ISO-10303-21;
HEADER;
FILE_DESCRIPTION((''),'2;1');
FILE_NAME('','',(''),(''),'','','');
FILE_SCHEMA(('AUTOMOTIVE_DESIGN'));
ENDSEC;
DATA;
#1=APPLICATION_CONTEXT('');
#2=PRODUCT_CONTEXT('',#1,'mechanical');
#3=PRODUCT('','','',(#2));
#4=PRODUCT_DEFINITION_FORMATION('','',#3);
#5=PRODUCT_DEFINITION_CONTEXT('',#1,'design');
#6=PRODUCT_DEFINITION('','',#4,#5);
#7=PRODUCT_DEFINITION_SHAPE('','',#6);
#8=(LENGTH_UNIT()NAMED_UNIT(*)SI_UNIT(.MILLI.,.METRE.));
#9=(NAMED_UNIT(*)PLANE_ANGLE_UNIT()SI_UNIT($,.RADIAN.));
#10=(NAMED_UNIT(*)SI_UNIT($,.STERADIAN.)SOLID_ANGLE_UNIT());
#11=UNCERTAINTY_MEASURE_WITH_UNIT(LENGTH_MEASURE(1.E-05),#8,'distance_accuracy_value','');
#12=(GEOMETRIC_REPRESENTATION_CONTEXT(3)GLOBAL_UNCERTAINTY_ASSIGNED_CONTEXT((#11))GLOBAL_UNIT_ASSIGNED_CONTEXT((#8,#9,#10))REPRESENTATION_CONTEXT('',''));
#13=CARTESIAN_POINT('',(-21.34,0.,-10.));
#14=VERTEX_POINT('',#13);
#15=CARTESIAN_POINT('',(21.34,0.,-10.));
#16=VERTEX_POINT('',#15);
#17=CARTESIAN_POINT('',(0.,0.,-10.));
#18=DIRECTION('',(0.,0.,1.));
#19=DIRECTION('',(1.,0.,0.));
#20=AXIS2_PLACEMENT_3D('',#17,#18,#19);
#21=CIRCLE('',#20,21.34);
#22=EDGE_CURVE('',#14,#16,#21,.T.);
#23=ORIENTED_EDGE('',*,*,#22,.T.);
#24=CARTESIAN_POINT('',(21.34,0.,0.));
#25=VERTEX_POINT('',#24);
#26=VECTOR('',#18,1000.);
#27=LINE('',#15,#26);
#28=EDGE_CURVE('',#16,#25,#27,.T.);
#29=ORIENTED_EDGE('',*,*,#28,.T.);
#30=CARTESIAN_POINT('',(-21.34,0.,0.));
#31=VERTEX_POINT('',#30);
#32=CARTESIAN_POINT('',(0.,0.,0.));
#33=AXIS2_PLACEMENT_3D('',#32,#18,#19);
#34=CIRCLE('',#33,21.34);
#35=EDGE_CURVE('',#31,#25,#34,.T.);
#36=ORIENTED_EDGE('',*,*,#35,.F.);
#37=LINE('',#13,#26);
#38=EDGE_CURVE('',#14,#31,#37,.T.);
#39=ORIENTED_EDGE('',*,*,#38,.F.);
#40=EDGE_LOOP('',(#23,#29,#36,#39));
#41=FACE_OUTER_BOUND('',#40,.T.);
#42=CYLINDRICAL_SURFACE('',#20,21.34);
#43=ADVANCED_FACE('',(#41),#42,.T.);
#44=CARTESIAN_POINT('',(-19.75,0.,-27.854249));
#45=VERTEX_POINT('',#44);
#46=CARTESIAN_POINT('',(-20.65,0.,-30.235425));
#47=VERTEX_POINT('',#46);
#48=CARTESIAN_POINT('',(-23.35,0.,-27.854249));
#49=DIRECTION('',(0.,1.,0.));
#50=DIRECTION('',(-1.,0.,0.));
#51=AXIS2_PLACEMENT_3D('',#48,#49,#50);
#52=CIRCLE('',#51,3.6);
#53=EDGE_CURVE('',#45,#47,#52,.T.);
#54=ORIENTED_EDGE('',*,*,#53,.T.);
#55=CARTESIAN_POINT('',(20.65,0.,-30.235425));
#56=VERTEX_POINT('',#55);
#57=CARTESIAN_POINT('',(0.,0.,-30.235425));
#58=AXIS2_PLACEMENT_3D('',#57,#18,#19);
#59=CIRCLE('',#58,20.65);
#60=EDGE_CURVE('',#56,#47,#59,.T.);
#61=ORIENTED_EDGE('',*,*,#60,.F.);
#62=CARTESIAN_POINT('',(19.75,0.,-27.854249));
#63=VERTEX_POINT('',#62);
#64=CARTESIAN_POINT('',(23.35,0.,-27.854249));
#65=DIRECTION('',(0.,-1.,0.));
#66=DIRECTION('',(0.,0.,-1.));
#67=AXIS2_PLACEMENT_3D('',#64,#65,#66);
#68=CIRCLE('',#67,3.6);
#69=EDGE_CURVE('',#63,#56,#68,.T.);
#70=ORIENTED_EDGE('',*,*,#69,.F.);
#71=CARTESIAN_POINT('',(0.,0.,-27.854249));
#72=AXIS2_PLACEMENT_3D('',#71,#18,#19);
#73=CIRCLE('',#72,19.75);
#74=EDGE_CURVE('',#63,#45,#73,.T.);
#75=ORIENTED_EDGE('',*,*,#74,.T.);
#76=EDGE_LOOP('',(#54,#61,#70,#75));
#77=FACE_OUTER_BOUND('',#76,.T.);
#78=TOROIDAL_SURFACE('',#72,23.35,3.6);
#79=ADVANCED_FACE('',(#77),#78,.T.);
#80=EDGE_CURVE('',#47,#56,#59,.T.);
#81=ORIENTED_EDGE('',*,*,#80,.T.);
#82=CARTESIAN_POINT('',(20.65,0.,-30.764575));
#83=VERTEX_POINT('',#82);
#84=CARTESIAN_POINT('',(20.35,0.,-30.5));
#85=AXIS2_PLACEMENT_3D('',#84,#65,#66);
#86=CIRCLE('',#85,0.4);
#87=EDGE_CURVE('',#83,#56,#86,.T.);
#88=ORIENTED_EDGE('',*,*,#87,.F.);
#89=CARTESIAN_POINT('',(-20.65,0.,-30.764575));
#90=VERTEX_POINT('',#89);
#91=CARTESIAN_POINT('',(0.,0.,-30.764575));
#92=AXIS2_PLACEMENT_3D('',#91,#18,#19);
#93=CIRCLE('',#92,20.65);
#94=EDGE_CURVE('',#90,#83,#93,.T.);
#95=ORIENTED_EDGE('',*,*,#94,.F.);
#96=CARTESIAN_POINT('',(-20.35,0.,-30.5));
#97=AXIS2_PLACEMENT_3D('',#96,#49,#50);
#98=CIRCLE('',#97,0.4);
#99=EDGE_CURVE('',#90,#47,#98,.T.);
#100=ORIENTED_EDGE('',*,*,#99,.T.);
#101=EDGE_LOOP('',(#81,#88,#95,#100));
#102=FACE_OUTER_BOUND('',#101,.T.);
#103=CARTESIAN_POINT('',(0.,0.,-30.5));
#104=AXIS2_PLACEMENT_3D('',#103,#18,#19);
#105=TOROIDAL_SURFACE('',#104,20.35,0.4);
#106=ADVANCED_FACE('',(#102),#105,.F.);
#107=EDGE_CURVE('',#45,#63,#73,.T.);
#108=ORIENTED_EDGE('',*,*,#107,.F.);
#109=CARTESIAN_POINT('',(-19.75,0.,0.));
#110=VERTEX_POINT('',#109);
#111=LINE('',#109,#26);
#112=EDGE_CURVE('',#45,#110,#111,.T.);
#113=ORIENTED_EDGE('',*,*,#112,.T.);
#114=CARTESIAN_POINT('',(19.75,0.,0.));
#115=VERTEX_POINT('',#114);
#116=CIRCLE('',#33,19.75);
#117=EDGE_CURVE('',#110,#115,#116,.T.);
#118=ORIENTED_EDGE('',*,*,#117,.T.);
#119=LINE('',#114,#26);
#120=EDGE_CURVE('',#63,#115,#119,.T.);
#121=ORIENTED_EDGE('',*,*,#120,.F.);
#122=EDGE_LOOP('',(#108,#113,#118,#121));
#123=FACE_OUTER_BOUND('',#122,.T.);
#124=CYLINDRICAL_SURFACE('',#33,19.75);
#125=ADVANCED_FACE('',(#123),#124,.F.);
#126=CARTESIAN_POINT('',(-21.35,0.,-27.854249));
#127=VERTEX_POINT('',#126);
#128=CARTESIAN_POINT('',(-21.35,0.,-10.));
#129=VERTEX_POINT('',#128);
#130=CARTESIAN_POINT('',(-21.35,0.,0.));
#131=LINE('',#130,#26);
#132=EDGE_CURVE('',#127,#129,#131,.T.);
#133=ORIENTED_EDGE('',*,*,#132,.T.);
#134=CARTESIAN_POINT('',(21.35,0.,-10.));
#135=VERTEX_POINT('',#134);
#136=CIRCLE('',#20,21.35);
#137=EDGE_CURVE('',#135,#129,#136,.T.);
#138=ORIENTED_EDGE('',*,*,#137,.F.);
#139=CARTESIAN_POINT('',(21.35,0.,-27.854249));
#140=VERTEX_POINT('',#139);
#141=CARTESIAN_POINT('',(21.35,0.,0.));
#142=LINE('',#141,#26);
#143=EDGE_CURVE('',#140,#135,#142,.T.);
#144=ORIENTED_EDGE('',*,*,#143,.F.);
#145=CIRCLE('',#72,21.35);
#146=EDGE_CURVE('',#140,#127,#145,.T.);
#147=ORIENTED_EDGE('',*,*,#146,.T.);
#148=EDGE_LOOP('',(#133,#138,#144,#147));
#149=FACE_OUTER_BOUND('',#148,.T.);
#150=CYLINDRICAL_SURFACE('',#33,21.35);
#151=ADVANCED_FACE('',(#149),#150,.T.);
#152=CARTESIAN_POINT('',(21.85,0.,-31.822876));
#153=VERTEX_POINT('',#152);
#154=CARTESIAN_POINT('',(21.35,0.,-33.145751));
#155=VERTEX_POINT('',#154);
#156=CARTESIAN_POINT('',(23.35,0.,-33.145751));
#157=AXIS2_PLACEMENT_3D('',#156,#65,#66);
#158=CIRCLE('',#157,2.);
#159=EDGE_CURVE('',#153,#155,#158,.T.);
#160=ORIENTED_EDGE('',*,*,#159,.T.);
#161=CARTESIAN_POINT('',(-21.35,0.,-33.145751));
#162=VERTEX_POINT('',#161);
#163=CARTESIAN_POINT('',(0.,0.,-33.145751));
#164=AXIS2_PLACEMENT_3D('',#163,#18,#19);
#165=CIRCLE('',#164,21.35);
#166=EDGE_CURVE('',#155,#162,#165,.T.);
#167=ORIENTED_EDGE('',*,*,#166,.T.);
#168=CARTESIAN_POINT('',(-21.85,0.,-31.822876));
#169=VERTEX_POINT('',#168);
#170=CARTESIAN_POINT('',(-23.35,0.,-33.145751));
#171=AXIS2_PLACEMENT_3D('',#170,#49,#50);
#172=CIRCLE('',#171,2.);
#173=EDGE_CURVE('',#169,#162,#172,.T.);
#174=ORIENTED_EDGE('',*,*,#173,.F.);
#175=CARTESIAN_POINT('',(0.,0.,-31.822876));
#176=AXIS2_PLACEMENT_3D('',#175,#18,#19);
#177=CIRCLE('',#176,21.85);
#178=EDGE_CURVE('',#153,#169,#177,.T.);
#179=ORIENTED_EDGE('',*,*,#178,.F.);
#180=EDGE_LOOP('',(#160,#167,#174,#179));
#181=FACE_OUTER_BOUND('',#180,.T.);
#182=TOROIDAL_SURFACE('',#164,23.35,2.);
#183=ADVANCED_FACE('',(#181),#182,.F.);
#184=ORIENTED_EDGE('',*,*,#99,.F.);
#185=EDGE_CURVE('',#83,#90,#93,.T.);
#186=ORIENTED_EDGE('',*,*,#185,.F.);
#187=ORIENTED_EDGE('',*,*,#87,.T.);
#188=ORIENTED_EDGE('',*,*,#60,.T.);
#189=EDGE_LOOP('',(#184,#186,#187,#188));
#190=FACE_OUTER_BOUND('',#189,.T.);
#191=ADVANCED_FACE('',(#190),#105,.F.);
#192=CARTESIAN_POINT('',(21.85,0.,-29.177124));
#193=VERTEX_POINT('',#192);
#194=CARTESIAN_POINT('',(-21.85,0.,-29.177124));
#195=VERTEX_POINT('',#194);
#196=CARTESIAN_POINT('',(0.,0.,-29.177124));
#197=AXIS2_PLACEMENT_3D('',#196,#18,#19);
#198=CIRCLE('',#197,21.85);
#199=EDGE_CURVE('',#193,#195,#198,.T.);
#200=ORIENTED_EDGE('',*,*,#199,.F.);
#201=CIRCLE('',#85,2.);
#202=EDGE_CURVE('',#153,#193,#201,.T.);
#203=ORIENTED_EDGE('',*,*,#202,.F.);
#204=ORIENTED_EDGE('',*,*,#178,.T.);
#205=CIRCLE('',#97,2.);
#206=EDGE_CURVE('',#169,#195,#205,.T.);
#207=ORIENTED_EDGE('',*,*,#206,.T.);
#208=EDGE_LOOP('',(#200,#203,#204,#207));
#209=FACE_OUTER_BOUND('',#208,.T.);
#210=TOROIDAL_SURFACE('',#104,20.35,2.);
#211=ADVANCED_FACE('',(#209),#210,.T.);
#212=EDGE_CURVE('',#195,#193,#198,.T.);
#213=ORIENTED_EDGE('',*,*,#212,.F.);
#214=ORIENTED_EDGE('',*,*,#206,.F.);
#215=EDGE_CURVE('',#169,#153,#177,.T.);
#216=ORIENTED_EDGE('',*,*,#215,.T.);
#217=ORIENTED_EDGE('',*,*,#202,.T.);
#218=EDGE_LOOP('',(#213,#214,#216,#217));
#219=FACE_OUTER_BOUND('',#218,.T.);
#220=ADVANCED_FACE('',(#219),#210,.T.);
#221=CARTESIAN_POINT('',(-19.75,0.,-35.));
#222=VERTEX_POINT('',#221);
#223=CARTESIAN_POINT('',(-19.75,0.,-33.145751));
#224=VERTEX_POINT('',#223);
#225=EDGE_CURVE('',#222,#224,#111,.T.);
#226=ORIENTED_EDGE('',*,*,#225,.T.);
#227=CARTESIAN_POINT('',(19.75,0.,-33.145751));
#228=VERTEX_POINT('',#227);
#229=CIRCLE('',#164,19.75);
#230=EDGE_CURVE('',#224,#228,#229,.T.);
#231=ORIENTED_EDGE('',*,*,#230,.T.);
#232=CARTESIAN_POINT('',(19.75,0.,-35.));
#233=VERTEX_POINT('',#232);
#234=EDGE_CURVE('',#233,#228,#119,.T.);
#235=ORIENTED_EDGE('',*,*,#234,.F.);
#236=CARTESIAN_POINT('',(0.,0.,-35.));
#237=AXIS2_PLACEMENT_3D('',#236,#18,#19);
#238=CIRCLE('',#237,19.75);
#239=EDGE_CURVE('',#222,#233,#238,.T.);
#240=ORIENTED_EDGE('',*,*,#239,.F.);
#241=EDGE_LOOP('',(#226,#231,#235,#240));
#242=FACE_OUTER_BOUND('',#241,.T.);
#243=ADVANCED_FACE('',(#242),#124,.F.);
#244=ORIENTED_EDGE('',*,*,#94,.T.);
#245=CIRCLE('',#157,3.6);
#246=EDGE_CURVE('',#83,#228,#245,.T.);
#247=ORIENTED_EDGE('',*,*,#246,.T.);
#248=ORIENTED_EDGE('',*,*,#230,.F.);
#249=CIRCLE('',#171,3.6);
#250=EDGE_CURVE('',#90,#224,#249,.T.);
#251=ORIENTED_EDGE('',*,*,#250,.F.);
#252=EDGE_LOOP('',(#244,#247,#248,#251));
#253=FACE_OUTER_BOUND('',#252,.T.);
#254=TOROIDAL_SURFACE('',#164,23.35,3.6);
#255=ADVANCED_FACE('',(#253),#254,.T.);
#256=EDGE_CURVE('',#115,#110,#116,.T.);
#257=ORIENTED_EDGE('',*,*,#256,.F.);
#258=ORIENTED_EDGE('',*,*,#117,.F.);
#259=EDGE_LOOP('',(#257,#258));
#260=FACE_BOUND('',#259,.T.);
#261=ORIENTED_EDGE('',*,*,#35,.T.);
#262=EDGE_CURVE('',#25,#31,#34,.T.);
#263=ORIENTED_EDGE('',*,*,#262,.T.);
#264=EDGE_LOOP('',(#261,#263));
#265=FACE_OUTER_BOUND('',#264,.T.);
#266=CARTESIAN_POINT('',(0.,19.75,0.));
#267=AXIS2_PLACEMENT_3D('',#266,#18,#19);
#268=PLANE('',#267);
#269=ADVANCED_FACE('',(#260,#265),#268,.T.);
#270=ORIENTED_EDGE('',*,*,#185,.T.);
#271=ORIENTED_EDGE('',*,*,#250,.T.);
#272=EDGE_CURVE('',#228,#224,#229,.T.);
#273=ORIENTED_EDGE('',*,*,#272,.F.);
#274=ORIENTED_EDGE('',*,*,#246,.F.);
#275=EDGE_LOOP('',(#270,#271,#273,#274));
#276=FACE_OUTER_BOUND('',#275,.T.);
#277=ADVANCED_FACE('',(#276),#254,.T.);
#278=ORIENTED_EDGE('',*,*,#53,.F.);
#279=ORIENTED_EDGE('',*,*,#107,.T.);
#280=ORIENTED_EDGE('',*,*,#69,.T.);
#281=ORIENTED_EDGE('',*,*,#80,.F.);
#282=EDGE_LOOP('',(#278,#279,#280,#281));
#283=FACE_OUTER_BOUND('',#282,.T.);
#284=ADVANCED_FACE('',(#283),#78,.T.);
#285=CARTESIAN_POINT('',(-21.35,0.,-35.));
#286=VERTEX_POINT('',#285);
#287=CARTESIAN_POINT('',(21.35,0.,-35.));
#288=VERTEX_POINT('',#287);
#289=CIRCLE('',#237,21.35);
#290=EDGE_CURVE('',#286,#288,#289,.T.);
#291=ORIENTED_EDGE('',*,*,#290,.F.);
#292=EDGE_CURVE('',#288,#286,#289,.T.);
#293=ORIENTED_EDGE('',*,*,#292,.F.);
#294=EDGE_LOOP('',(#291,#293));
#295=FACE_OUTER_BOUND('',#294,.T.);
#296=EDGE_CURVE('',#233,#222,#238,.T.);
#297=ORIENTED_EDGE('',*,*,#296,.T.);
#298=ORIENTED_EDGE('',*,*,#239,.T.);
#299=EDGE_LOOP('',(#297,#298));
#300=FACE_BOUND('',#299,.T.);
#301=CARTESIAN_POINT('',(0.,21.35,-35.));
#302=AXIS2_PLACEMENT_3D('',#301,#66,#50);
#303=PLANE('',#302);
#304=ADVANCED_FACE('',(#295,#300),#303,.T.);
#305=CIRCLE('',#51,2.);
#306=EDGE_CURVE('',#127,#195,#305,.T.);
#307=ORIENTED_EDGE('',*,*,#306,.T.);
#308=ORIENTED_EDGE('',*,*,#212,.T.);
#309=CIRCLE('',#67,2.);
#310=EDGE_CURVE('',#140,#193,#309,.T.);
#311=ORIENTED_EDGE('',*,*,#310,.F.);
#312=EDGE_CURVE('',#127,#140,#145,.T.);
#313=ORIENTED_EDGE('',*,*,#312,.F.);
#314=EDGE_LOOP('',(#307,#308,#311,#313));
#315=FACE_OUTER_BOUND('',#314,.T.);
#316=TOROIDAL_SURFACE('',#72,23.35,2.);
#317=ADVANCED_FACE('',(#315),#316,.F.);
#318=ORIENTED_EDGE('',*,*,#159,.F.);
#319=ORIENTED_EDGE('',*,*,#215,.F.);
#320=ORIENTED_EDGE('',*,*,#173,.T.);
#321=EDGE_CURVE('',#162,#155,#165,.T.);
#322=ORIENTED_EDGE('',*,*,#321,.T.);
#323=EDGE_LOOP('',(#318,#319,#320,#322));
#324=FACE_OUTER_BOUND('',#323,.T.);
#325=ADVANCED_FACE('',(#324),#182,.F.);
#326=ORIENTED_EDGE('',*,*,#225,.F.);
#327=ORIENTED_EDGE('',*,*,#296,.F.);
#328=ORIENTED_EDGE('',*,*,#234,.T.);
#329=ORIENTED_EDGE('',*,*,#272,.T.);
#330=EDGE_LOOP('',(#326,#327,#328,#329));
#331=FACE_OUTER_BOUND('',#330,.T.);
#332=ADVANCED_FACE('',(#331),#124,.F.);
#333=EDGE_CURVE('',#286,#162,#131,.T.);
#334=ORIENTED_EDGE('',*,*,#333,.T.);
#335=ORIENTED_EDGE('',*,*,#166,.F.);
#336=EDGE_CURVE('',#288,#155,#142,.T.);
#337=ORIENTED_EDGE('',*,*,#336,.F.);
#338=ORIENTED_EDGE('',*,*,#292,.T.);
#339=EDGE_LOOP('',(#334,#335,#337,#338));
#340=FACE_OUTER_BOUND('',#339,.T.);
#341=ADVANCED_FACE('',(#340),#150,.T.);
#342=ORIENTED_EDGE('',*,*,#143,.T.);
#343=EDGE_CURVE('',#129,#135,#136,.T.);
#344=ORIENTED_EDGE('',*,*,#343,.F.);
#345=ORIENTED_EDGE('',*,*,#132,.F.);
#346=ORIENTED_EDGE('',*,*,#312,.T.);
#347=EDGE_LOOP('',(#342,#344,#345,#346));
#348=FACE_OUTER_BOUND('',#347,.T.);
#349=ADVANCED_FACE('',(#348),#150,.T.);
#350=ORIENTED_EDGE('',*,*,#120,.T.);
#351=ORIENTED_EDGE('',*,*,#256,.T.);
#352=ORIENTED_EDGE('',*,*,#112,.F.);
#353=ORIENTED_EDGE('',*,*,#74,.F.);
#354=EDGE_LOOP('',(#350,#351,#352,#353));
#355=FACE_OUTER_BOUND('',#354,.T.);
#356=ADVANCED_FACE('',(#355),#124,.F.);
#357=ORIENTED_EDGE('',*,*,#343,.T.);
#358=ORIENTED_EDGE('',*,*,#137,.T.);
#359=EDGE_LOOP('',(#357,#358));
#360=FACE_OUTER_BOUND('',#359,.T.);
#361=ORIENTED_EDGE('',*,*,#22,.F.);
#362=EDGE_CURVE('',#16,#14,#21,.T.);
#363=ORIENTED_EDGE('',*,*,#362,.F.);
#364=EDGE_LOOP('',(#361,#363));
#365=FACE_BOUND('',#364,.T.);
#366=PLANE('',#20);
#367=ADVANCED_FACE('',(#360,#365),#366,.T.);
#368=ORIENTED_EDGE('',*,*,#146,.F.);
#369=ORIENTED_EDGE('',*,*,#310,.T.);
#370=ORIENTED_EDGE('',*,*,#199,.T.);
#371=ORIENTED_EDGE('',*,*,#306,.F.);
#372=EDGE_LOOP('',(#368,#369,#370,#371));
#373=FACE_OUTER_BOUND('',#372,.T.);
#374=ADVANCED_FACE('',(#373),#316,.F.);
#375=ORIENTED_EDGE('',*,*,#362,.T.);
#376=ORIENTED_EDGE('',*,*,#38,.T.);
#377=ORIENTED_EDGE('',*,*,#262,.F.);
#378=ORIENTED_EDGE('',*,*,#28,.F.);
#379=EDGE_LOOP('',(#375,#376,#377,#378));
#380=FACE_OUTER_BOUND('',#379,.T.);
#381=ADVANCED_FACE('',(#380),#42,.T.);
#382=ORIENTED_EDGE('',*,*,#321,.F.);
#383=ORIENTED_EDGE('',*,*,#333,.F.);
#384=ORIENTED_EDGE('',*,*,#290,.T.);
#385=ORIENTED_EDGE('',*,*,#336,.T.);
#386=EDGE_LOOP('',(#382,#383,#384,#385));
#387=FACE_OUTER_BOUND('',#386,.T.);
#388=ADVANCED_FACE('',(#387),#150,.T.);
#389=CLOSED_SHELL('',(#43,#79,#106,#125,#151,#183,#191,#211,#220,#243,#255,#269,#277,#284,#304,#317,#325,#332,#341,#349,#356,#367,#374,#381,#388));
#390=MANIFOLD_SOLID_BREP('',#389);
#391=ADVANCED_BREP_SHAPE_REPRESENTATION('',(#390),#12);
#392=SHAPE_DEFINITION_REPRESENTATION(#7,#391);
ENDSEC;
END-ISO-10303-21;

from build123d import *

# Parameters (mm, degrees)
CUT_EXTRUDE1_START = -10
SKETCH2_R          = 21.35
SKETCH2_R_2        = 21.34
CUT_EXTRUDE1_DEPTH = 10


with BuildPart() as part:
    # Sketch1 → Revolve-Thin1 (revolve)
    with BuildSketch(Plane(origin=(0, 0, 0), x_dir=(0, 0, -1), z_dir=(1, 0, 0)), mode=Mode.PRIVATE) as revolve_thin1_sk:
        with BuildLine():
            Line((0, 21.35), (27.854248689, 21.35))
            ThreePointArc((27.854248689, 21.35), (28.56135547, 21.479171307), (29.177124344, 21.85))
            ThreePointArc((29.177124344, 21.85), (30.5, 22.35), (31.822875656, 21.85))
            ThreePointArc((31.822875656, 21.85), (32.43864453, 21.479171307), (33.145751311, 21.35))
            Line((33.145751311, 21.35), (35, 21.35))
            Line((35, 21.35), (35, 19.75))
            Line((35, 19.75), (33.145751311, 19.75))
            ThreePointArc((33.145751311, 19.75), (31.872959105, 19.982508352), (30.764575131, 20.65))
            ThreePointArc((30.764575131, 20.65), (30.5, 20.75), (30.235424869, 20.65))
            ThreePointArc((30.235424869, 20.65), (29.127040895, 19.982508352), (27.854248689, 19.75))
            Line((27.854248689, 19.75), (0, 19.75))
            Line((0, 19.75), (0, 21.35))
        make_face()
    revolve(revolve_thin1_sk.sketch.rotate(Axis((0, 0, 0), (0, 0, -1)), 90), axis=Axis((0, 0, 0), (0, 0, -1)))

    # Sketch2 → Cut-Extrude1 (cut)
    with BuildSketch(Plane.XY.offset(CUT_EXTRUDE1_START)):
        Circle(SKETCH2_R)
        Circle(SKETCH2_R_2, mode=Mode.SUBTRACT)
    extrude(amount=CUT_EXTRUDE1_DEPTH, mode=Mode.SUBTRACT)


solid = part.part
